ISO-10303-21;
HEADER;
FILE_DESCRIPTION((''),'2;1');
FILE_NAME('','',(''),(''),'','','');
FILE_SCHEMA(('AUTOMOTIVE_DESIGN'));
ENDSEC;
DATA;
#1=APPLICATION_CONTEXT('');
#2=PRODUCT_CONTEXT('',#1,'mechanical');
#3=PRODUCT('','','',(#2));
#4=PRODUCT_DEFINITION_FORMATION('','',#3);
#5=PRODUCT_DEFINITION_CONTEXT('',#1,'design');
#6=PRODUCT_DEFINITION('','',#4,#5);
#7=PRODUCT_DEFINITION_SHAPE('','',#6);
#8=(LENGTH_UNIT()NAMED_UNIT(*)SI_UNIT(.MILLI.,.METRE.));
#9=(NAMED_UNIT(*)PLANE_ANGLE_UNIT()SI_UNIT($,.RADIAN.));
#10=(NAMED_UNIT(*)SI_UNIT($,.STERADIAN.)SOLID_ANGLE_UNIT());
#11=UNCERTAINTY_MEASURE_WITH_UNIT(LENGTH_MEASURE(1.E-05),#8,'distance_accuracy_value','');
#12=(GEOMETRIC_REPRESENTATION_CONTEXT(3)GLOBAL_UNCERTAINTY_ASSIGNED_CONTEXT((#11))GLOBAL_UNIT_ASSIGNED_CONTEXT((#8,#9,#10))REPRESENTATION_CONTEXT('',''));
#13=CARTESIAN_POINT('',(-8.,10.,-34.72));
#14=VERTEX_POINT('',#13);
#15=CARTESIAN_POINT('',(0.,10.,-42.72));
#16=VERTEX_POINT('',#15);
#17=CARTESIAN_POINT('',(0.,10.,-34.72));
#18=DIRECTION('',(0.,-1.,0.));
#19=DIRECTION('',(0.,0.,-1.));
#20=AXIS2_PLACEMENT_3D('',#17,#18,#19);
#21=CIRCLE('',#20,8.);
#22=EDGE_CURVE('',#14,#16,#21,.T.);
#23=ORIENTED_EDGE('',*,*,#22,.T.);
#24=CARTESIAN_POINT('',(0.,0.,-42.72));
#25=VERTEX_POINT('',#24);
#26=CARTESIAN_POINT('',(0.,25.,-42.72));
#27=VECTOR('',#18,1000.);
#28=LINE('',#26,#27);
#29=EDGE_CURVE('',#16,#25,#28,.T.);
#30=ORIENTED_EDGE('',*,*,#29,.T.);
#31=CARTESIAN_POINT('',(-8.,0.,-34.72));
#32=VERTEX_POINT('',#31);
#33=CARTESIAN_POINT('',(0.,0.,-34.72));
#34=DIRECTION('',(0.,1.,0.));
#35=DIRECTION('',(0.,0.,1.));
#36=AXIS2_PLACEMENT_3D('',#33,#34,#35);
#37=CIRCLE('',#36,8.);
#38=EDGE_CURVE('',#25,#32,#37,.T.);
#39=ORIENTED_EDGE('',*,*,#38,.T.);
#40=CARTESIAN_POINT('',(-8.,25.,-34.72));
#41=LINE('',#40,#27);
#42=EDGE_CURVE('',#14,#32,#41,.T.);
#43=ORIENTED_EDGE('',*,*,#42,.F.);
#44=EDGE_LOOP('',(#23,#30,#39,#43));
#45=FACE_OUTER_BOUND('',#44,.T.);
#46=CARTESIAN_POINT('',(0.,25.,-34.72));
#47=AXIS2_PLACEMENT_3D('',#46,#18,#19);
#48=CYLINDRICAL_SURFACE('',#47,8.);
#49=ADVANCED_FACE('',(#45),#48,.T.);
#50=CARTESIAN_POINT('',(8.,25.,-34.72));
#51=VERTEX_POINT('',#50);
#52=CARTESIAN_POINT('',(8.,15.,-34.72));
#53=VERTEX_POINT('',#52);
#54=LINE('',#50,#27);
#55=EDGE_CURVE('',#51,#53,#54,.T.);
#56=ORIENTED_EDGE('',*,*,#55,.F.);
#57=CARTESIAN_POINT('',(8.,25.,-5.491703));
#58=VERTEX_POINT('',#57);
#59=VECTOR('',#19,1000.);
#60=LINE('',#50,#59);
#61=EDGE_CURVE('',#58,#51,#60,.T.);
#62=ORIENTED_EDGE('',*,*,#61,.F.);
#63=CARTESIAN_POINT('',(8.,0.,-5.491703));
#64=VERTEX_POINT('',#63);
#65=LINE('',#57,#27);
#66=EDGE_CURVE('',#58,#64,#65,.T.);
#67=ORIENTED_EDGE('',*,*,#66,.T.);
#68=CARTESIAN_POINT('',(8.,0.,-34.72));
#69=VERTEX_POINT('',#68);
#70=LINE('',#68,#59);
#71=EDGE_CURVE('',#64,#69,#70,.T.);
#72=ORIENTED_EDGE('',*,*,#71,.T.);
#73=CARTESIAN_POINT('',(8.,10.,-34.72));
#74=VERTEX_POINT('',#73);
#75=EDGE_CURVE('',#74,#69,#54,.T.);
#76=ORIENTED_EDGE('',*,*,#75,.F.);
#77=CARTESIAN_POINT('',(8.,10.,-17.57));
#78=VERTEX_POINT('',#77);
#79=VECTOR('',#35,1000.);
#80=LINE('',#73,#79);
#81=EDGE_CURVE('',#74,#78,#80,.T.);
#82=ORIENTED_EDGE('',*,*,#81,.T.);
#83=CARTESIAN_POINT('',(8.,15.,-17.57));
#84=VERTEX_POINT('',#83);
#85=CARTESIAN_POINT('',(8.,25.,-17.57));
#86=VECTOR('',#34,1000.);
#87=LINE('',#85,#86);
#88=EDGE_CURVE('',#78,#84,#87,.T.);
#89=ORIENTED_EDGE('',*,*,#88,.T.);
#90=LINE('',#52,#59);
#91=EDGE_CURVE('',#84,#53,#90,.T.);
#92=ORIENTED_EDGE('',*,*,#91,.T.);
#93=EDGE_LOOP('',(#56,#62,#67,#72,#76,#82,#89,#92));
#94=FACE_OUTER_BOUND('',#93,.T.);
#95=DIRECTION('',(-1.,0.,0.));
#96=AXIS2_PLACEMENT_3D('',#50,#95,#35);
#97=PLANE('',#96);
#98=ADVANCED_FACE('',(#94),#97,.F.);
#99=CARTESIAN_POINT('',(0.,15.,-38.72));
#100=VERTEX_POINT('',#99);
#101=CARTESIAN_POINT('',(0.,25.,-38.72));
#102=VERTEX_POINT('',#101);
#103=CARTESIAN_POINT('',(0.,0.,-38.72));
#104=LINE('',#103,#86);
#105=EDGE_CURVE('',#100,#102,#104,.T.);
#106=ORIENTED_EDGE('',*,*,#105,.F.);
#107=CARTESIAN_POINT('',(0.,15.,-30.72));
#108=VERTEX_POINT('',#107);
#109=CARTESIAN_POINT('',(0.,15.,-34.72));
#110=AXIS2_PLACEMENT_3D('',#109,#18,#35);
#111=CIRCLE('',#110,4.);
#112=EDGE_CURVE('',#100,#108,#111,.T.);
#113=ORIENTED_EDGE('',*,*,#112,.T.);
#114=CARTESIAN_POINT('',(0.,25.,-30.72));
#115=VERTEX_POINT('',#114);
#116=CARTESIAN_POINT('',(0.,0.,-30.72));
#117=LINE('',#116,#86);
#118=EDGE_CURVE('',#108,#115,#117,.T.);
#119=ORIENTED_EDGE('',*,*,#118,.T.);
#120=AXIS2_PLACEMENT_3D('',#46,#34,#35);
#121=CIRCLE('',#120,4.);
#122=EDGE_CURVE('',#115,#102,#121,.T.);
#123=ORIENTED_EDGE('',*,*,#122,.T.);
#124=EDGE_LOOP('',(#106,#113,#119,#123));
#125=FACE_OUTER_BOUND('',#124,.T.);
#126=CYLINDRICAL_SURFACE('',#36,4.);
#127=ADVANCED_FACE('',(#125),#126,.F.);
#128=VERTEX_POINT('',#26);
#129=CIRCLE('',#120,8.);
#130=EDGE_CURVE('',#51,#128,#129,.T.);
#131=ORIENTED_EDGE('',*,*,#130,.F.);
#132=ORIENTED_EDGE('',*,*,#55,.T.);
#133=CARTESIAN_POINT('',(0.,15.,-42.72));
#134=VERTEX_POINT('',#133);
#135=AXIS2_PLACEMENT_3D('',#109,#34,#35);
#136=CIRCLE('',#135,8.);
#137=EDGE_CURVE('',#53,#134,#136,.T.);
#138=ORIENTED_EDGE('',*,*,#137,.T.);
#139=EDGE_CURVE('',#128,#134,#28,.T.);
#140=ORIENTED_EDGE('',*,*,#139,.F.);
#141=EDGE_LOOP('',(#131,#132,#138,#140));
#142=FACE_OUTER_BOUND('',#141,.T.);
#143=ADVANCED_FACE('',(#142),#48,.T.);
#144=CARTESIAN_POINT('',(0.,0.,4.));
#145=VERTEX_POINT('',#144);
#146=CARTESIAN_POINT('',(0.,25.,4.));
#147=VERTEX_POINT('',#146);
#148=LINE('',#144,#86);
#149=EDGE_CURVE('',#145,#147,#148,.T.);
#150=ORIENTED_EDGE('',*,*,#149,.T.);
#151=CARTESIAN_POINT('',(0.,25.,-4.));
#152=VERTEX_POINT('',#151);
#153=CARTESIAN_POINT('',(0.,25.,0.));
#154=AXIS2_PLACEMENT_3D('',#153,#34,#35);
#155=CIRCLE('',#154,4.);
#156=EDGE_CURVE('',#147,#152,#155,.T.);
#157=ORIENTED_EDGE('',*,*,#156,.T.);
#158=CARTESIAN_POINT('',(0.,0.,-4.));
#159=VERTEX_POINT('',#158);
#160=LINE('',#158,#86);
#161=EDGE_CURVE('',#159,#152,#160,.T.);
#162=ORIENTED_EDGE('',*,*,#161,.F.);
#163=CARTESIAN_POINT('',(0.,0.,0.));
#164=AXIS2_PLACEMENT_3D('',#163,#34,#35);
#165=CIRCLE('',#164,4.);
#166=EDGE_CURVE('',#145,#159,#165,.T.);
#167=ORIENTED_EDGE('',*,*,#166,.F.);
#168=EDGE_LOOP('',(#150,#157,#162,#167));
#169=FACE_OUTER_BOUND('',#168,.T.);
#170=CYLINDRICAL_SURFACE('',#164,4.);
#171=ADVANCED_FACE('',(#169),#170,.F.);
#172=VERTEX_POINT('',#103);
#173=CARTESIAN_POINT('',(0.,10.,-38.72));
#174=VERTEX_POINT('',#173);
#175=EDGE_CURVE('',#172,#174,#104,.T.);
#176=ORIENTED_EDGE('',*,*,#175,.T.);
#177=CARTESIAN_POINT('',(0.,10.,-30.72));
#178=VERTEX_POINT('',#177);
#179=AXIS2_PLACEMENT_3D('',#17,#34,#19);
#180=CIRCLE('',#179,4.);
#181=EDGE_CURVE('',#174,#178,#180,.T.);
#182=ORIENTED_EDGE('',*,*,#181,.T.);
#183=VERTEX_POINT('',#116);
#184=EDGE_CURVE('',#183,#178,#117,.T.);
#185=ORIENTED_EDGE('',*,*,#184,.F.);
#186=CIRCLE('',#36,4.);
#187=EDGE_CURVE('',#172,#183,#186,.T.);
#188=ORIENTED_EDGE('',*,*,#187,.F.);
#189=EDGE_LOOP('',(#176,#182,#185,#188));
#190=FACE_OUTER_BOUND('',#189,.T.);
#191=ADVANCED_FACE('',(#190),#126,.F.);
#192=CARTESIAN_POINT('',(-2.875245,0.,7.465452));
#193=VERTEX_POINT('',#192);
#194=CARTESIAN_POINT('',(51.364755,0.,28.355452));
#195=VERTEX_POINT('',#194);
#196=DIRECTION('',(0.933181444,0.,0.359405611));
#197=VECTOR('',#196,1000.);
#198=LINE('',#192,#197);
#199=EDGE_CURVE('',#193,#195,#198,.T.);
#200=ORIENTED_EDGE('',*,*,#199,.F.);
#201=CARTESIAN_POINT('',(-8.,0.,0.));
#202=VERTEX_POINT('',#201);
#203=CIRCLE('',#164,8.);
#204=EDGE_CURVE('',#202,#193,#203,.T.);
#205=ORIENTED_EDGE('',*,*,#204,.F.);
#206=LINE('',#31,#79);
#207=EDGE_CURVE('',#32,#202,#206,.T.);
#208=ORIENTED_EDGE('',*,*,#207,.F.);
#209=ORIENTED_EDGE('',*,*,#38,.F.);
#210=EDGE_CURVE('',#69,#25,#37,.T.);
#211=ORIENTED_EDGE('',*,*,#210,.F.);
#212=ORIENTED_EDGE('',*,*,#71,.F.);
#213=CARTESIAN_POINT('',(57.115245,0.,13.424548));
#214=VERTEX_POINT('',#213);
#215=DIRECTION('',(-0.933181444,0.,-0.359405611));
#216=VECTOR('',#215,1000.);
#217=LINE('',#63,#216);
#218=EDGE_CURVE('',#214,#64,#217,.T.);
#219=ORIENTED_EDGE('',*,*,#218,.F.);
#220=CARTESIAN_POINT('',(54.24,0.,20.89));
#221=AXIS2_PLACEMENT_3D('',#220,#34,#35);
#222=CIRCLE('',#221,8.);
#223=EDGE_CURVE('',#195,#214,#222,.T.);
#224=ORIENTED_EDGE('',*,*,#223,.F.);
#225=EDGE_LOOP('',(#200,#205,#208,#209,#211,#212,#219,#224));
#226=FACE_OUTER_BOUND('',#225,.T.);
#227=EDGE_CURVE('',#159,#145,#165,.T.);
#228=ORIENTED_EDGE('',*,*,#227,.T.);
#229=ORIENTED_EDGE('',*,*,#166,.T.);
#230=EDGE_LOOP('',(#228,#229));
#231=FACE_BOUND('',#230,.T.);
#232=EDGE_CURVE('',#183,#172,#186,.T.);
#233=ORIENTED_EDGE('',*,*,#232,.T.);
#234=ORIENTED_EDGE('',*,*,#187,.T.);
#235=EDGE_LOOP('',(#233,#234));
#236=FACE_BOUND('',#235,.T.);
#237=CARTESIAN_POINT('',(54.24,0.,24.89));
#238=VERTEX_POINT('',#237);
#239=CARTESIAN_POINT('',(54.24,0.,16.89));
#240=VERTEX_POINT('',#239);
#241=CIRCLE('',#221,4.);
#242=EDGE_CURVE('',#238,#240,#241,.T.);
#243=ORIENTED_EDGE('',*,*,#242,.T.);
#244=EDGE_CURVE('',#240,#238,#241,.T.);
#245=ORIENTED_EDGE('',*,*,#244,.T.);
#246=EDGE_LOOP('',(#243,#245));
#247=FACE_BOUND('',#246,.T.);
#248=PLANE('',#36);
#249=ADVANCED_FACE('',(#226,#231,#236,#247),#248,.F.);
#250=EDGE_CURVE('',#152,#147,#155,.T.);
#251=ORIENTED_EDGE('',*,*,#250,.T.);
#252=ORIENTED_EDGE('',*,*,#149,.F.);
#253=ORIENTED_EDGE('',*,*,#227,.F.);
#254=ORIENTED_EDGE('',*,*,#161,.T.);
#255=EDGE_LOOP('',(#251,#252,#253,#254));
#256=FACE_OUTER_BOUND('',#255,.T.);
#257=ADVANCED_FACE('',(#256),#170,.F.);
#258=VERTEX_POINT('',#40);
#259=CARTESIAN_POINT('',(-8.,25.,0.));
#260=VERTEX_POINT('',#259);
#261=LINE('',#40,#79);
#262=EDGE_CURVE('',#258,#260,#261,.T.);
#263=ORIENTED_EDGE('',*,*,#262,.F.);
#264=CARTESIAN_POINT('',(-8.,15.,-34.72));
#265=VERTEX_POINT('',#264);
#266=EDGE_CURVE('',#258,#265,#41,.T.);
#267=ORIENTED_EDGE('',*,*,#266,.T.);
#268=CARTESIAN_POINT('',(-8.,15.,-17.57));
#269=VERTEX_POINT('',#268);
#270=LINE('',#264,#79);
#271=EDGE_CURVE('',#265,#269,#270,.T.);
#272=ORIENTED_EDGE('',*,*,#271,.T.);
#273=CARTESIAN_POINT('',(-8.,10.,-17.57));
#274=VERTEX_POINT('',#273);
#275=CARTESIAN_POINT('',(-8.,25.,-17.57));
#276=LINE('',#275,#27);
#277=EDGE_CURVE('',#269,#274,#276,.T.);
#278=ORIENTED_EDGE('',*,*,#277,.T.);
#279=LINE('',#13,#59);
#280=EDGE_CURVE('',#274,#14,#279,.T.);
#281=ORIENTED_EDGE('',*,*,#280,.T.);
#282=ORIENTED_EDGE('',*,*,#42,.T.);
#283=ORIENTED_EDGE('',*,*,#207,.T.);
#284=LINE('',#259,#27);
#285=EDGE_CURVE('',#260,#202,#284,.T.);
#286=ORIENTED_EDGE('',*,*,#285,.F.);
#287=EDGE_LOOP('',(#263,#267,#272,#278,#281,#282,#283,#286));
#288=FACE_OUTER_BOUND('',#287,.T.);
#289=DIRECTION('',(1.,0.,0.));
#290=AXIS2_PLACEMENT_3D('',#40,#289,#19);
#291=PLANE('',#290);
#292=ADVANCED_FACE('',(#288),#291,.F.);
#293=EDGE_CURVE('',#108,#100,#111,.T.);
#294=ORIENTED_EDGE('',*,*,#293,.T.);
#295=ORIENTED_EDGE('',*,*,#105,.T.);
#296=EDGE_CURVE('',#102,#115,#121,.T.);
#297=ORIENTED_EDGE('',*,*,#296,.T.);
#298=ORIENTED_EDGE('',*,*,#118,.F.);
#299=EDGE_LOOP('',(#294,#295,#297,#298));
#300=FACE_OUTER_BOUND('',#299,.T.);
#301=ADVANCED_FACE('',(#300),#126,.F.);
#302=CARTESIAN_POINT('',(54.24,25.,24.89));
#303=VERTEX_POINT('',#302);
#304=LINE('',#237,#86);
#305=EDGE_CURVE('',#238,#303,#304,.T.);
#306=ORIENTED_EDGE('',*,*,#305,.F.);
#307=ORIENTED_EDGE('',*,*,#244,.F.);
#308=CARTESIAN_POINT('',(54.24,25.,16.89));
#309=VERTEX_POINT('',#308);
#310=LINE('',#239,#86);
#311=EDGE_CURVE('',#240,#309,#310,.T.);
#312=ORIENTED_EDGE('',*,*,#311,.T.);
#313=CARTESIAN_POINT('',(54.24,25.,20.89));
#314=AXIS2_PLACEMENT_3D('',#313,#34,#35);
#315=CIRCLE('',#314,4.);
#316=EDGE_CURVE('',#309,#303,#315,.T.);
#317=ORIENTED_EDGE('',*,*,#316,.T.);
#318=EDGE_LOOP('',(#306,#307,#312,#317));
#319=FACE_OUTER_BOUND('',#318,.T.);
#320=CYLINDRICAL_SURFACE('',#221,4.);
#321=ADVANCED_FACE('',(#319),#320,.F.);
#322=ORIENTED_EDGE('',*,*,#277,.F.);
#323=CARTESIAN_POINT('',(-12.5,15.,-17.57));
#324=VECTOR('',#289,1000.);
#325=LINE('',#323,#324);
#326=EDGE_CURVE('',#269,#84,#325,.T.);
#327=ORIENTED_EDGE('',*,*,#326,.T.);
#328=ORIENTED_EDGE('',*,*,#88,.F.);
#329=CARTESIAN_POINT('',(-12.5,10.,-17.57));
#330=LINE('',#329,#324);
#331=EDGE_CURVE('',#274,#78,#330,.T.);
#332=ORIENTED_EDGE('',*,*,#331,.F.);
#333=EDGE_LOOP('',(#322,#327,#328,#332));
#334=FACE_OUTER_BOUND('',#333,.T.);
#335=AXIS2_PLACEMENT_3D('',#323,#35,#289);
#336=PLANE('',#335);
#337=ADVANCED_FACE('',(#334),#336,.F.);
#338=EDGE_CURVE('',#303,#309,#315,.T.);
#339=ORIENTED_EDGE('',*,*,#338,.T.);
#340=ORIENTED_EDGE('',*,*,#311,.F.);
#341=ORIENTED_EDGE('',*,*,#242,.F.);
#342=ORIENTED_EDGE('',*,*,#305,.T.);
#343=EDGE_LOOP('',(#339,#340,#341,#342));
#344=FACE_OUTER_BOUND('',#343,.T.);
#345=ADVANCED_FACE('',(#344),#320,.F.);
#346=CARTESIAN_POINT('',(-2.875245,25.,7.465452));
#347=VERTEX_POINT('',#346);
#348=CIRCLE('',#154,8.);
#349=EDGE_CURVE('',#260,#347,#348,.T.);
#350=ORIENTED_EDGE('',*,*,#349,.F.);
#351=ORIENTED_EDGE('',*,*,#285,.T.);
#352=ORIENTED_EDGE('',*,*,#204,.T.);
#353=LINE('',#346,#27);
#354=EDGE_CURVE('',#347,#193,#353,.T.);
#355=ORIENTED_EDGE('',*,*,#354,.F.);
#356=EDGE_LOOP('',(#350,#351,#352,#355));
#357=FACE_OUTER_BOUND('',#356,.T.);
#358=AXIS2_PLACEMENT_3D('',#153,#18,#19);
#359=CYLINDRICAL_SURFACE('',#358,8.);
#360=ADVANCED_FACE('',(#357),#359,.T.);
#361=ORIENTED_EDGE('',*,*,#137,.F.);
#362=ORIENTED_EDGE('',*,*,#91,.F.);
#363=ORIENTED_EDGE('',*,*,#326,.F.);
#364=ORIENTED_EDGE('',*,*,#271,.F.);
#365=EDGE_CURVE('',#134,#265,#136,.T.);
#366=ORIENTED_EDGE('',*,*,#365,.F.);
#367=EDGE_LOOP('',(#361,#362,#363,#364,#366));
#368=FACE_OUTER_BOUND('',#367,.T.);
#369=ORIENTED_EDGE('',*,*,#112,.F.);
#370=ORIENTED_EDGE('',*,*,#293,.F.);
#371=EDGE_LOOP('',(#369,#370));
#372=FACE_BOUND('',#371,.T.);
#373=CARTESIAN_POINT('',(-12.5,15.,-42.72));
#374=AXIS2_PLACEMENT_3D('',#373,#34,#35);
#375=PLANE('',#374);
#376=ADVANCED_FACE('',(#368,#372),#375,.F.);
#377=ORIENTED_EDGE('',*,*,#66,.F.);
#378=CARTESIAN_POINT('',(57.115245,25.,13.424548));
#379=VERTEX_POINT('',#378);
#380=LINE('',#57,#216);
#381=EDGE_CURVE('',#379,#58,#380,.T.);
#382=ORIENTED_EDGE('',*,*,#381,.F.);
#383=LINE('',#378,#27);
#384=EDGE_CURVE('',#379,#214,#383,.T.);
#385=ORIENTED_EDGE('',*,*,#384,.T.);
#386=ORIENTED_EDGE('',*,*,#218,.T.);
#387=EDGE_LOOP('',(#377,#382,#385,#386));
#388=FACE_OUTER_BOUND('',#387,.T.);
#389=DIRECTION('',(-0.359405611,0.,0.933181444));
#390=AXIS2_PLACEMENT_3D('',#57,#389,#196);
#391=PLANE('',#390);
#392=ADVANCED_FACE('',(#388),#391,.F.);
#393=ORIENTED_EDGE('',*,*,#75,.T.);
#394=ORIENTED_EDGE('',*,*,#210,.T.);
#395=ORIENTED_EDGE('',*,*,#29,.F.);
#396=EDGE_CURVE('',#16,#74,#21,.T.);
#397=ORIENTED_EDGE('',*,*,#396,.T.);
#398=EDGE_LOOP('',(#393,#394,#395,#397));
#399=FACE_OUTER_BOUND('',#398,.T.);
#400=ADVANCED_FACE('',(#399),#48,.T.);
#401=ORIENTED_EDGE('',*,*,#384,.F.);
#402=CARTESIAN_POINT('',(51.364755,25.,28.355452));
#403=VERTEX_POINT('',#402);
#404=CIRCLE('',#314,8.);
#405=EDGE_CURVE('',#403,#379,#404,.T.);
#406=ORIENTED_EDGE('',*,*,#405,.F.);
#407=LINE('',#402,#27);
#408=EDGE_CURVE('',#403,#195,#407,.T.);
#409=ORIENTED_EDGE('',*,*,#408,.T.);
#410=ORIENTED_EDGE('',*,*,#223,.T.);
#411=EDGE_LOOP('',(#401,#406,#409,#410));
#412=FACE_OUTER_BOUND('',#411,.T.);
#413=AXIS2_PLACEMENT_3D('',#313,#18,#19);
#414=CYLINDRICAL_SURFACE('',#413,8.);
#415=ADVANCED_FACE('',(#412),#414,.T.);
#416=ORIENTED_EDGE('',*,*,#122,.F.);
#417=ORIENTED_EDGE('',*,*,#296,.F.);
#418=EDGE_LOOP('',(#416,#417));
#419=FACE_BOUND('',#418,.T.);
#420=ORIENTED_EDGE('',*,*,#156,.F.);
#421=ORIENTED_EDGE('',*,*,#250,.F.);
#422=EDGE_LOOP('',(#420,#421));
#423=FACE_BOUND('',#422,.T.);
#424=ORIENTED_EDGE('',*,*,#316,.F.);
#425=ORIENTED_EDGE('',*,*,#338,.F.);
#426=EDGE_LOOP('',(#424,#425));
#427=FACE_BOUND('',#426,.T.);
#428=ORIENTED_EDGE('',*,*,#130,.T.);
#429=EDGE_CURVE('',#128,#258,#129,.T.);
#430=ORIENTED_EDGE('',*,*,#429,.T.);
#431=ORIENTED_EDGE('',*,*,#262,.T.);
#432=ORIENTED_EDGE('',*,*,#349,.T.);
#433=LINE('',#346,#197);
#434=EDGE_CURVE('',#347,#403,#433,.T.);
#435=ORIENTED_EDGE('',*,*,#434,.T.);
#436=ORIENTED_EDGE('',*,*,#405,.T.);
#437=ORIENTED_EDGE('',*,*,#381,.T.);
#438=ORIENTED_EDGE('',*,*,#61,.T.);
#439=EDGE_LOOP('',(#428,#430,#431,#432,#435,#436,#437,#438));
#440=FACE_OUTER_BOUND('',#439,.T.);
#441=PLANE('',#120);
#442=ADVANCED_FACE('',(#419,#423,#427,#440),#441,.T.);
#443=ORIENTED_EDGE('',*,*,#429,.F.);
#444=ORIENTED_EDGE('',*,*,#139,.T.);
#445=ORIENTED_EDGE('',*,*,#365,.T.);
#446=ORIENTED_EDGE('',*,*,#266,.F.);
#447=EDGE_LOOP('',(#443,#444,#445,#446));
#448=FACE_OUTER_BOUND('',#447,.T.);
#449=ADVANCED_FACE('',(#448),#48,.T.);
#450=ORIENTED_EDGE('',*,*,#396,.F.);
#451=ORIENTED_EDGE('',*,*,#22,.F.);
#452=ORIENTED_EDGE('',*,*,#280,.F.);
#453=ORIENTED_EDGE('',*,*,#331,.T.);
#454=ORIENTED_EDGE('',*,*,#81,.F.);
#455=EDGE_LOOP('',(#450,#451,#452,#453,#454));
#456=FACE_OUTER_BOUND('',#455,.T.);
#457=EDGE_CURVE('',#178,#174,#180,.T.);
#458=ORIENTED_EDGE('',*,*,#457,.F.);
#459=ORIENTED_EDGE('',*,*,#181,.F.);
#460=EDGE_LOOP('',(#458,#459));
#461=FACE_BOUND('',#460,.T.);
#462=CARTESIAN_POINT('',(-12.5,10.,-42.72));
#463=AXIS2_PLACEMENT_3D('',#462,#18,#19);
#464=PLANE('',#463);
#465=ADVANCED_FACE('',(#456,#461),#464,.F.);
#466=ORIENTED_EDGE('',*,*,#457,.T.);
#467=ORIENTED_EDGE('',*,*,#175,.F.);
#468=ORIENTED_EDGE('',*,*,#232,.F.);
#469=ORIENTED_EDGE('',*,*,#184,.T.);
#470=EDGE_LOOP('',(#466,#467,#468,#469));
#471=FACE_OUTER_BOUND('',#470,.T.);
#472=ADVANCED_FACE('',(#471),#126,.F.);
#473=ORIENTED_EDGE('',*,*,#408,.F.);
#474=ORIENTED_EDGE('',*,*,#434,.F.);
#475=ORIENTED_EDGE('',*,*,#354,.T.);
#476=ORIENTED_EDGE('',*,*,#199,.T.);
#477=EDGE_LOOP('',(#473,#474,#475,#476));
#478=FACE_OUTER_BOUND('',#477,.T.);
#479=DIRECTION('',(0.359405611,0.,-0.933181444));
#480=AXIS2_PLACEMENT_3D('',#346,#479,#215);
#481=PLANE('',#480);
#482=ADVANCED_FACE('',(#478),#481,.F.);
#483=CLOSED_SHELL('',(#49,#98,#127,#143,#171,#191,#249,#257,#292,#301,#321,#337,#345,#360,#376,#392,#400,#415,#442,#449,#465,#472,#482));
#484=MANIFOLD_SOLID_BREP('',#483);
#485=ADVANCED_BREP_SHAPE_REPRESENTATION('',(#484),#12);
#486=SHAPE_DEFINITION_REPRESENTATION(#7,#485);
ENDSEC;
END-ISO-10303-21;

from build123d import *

# Parameters (mm, degrees)
L_BRACKET_BODY_DEPTH   = 25
PIVOT_HOLES_SKETCH_R   = 4
PIVOT_HOLES_3X_8_DEPTH = 25
CLEVIS_SLOT_SKETCH_W   = 25.15
CLEVIS_SLOT_SKETCH_H   = 5
CLEVIS_SLOT_5MM_DEPTH  = 12.5


with BuildPart() as part:
    # Bracket Profile Sketch → L Bracket Body (new body)
    with BuildSketch(Plane(origin=(0, 0, 0), x_dir=(1, 0, 0), z_dir=(0, 1, 0))):
        with BuildLine():
            Line((8, 34.72), (8, 5.491702761))
            Line((8, 5.491702761), (57.11524489, -13.424548452))
            ThreePointArc((57.11524489, -13.424548452), (61.705451548, -23.76524489), (51.36475511, -28.355451548))
            Line((51.36475511, -28.355451548), (-2.87524489, -7.465451548))
            ThreePointArc((-2.87524489, -7.465451548), (-6.595527239, -4.527584393), (-8, 0))
            Line((-8, 0), (-8, 34.72))
            ThreePointArc((-8, 34.72), (0, 42.72), (8, 34.72))
        make_face()
    extrude(amount=L_BRACKET_BODY_DEPTH)

    # Pivot Holes Sketch → Pivot Holes 3xØ8 (cut)
    with BuildSketch(Plane(origin=(0, 25, 0), x_dir=(1, 0, 0), z_dir=(0, 1, 0))):
        with Locations(Location((0, 34.72, 0), (0, 0, 270))):
            Circle(PIVOT_HOLES_SKETCH_R)
        with Locations(Location((54.24, -20.89, 0), (0, 0, 270))):
            Circle(PIVOT_HOLES_SKETCH_R)
        with Locations(Location((0, 0, 0), (0, 0, 270))):
            Circle(PIVOT_HOLES_SKETCH_R)
    extrude(amount=-PIVOT_HOLES_3X_8_DEPTH, mode=Mode.SUBTRACT)

    # Clevis Slot Sketch → Clevis Slot 5mm (cut, symmetric)
    with BuildSketch(Plane(origin=(0, 0, 0), x_dir=(0, 0, -1), z_dir=(1, 0, 0))):
        with Locations((30.145, 12.5)):
            Rectangle(CLEVIS_SLOT_SKETCH_W, CLEVIS_SLOT_SKETCH_H)
    extrude(amount=CLEVIS_SLOT_5MM_DEPTH, both=True, mode=Mode.SUBTRACT)


solid = part.part
